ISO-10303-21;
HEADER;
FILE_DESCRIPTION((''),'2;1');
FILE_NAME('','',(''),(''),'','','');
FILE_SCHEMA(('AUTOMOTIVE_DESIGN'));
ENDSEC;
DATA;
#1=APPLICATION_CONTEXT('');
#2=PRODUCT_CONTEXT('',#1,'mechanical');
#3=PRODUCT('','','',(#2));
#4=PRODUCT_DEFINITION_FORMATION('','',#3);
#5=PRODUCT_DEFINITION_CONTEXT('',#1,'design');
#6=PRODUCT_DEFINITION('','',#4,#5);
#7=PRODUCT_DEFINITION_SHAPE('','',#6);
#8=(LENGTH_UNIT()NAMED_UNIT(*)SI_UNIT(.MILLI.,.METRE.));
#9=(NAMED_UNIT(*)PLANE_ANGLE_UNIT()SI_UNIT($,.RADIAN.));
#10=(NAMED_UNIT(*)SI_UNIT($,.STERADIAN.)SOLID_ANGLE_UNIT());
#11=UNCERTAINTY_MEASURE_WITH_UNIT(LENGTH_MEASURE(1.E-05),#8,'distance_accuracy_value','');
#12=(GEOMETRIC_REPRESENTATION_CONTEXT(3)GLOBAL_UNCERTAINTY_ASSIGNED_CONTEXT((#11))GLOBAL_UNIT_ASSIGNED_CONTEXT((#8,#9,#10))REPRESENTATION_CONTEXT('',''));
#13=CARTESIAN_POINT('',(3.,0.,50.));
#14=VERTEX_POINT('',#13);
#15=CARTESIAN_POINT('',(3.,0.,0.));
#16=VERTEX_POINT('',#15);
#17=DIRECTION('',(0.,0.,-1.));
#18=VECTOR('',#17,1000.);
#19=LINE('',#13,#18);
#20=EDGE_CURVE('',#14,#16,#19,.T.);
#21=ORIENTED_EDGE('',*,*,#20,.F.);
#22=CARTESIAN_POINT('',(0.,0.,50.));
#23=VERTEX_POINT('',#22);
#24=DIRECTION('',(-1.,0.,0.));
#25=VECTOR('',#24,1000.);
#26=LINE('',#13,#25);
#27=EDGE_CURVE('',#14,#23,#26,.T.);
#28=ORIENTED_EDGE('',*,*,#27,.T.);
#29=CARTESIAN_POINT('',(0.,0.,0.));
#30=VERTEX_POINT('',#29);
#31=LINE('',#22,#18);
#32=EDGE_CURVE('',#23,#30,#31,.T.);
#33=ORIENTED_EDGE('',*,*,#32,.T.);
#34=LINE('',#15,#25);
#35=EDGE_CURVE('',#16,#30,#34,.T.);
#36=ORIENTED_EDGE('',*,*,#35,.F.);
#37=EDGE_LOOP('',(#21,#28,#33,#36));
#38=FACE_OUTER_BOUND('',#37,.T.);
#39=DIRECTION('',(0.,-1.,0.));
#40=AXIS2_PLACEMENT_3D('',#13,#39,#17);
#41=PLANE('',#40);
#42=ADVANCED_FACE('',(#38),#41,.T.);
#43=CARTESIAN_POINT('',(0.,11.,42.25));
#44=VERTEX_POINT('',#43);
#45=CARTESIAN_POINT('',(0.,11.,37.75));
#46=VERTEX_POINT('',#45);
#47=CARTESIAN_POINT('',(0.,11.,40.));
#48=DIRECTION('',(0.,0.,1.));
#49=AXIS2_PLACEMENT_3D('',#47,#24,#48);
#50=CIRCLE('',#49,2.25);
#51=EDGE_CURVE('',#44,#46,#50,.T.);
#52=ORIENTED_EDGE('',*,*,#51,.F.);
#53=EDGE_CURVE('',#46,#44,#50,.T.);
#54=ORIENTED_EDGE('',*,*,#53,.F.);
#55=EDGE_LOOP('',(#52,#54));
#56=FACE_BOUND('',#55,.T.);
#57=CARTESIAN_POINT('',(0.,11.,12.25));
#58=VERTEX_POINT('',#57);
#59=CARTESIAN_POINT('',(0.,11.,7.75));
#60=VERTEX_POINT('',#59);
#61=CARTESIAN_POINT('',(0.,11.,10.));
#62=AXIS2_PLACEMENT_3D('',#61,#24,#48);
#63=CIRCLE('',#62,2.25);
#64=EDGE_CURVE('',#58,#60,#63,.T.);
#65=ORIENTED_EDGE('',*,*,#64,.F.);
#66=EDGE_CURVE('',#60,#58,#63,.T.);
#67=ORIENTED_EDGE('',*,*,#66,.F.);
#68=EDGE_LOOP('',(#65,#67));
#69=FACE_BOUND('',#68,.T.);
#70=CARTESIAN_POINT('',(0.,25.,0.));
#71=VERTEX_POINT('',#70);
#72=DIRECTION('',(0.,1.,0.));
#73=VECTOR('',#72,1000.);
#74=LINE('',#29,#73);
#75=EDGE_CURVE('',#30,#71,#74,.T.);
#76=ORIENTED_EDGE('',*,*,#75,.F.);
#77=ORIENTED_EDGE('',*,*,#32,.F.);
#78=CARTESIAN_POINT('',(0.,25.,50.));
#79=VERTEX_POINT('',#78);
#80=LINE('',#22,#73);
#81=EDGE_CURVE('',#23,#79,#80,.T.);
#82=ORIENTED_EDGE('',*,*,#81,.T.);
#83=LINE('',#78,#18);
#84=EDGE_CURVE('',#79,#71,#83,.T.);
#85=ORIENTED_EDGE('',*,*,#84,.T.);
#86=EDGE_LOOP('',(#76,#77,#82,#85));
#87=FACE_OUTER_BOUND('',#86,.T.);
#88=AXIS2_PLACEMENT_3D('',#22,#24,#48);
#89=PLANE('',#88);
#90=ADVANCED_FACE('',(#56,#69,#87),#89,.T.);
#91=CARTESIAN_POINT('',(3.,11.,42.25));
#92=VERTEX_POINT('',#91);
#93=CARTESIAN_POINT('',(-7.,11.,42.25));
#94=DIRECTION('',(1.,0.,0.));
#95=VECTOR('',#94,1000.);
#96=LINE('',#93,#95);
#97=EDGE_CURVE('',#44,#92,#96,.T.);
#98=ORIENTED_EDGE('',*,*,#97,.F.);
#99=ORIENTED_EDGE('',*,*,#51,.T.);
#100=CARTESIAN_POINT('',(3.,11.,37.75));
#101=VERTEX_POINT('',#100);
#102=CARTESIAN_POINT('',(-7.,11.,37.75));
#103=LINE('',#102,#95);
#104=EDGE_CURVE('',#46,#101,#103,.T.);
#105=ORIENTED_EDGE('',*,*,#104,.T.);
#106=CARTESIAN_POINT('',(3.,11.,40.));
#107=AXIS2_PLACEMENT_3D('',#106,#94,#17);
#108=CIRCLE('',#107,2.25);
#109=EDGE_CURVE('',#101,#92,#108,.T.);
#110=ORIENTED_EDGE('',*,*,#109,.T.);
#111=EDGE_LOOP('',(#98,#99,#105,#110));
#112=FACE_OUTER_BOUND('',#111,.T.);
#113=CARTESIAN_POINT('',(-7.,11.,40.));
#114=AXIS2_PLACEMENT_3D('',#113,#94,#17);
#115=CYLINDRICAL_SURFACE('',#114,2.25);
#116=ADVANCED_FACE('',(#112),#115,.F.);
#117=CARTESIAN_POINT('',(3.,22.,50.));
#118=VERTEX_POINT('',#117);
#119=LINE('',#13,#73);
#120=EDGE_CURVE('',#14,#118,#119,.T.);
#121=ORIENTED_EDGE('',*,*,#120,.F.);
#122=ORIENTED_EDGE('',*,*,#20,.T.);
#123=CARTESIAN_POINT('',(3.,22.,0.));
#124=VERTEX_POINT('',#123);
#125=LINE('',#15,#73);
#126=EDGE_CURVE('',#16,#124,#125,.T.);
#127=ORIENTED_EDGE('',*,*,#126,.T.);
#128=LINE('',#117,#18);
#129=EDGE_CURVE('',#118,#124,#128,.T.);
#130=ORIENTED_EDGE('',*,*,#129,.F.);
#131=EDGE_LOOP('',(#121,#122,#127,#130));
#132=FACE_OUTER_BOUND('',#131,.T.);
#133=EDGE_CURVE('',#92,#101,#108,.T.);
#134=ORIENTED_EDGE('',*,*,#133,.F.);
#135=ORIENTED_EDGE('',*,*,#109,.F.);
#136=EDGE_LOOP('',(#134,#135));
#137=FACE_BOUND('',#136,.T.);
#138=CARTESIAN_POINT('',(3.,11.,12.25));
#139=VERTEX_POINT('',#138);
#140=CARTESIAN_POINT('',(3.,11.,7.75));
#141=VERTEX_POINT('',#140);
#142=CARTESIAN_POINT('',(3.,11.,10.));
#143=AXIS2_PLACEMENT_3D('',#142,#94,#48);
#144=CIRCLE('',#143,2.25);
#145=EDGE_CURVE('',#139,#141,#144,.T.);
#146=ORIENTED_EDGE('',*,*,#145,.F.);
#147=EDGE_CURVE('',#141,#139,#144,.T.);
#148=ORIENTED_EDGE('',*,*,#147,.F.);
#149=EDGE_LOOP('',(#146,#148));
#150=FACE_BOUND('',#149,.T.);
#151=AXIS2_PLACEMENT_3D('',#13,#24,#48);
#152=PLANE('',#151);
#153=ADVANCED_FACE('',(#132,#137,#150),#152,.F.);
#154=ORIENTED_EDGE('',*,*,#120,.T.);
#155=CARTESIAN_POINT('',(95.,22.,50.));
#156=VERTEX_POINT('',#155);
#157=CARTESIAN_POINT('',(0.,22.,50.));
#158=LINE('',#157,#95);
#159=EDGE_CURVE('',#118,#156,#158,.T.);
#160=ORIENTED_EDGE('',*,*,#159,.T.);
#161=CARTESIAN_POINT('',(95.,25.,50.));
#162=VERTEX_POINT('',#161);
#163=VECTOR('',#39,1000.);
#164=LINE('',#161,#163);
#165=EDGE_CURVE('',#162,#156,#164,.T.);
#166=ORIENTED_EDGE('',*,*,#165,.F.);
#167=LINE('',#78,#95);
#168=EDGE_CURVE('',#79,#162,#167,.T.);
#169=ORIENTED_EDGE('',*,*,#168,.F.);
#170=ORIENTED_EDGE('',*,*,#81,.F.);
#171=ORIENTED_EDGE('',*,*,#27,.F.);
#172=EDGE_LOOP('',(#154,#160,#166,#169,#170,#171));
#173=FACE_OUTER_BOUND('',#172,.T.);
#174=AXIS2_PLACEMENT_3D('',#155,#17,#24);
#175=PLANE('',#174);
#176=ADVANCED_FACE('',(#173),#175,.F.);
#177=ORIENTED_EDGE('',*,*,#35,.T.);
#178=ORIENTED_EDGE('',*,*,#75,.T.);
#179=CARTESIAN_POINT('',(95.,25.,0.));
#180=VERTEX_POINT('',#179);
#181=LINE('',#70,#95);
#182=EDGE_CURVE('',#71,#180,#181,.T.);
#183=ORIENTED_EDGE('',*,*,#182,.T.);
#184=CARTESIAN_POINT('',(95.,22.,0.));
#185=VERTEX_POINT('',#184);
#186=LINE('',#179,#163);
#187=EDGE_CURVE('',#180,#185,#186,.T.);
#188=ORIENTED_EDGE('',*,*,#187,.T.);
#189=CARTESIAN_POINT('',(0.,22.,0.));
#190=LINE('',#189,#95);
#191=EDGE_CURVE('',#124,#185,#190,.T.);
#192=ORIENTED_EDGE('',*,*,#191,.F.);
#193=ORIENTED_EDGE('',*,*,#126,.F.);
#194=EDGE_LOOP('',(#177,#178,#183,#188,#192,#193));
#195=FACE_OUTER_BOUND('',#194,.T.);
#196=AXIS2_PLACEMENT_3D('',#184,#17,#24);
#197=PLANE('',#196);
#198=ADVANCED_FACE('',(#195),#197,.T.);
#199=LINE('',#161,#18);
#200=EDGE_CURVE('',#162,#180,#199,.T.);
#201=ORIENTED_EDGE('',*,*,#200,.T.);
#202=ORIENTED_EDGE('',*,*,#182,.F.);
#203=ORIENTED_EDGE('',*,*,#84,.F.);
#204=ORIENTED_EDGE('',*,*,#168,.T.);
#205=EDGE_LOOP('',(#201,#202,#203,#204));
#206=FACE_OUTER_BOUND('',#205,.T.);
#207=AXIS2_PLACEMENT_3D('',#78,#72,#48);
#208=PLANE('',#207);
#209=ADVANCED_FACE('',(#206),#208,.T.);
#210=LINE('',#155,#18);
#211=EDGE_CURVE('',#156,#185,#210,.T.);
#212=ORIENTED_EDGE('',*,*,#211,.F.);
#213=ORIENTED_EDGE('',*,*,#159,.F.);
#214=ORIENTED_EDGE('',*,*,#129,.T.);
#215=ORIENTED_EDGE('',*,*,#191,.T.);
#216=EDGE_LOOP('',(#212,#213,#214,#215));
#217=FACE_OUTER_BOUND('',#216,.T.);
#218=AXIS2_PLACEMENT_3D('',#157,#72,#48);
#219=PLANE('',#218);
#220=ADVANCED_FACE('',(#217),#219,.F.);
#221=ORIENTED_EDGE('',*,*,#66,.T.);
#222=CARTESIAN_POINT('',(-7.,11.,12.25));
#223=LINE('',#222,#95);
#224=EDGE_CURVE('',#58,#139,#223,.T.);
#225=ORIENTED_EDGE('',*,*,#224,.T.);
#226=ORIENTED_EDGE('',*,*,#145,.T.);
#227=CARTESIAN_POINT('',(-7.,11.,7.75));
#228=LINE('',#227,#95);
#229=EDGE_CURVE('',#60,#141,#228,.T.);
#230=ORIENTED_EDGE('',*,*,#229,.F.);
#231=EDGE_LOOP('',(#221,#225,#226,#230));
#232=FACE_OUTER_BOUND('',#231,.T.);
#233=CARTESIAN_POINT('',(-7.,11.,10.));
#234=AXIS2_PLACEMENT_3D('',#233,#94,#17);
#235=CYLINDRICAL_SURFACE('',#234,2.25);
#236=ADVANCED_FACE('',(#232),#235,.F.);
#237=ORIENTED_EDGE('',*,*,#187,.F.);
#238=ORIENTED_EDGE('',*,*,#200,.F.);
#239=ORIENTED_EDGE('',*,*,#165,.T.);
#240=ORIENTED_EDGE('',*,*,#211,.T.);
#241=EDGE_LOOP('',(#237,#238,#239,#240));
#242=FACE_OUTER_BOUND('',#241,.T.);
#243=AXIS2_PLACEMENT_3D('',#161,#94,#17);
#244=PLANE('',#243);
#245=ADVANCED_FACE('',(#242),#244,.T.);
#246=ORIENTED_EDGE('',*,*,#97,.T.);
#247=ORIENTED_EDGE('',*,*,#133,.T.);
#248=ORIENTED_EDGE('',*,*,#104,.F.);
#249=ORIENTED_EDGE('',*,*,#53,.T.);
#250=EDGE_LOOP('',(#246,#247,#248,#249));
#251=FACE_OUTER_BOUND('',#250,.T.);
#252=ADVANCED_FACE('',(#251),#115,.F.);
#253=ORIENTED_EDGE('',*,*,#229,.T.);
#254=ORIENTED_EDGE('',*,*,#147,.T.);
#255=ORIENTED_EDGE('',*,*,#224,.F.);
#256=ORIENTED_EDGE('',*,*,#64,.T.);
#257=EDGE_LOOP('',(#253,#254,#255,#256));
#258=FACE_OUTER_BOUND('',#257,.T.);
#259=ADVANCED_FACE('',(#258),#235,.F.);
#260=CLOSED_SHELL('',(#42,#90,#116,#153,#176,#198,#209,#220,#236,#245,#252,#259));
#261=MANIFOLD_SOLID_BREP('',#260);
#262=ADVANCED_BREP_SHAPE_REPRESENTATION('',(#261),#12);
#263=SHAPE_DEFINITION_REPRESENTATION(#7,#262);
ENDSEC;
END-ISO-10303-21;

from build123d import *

# Parameters (mm, degrees)
EXTRUDE_1_DEPTH     = 50
SKETCH_2_R          = 2.25
CUT_EXTRUDE_1_DEPTH = 10


with BuildPart() as part:
    # 草图1 → 拉伸-薄壁1 (new body)
    with BuildSketch(Plane.XY):
        Polygon((0, 0), (0, 25), (95, 25), (95, 22), (3, 22), (3, 0), align=None)
    extrude(amount=EXTRUDE_1_DEPTH)

    # 草图2 → 切除-拉伸1 (cut)
    with BuildSketch(Plane(origin=(3, 0, 0), x_dir=(0, 0, -1), z_dir=(1, 0, 0))):
        with Locations((-40, 11)):
            Circle(SKETCH_2_R)
        with Locations(Location((-10, 11, 0), (0, 0, 180))):
            Circle(SKETCH_2_R)
    extrude(amount=-CUT_EXTRUDE_1_DEPTH, mode=Mode.SUBTRACT)


solid = part.part
